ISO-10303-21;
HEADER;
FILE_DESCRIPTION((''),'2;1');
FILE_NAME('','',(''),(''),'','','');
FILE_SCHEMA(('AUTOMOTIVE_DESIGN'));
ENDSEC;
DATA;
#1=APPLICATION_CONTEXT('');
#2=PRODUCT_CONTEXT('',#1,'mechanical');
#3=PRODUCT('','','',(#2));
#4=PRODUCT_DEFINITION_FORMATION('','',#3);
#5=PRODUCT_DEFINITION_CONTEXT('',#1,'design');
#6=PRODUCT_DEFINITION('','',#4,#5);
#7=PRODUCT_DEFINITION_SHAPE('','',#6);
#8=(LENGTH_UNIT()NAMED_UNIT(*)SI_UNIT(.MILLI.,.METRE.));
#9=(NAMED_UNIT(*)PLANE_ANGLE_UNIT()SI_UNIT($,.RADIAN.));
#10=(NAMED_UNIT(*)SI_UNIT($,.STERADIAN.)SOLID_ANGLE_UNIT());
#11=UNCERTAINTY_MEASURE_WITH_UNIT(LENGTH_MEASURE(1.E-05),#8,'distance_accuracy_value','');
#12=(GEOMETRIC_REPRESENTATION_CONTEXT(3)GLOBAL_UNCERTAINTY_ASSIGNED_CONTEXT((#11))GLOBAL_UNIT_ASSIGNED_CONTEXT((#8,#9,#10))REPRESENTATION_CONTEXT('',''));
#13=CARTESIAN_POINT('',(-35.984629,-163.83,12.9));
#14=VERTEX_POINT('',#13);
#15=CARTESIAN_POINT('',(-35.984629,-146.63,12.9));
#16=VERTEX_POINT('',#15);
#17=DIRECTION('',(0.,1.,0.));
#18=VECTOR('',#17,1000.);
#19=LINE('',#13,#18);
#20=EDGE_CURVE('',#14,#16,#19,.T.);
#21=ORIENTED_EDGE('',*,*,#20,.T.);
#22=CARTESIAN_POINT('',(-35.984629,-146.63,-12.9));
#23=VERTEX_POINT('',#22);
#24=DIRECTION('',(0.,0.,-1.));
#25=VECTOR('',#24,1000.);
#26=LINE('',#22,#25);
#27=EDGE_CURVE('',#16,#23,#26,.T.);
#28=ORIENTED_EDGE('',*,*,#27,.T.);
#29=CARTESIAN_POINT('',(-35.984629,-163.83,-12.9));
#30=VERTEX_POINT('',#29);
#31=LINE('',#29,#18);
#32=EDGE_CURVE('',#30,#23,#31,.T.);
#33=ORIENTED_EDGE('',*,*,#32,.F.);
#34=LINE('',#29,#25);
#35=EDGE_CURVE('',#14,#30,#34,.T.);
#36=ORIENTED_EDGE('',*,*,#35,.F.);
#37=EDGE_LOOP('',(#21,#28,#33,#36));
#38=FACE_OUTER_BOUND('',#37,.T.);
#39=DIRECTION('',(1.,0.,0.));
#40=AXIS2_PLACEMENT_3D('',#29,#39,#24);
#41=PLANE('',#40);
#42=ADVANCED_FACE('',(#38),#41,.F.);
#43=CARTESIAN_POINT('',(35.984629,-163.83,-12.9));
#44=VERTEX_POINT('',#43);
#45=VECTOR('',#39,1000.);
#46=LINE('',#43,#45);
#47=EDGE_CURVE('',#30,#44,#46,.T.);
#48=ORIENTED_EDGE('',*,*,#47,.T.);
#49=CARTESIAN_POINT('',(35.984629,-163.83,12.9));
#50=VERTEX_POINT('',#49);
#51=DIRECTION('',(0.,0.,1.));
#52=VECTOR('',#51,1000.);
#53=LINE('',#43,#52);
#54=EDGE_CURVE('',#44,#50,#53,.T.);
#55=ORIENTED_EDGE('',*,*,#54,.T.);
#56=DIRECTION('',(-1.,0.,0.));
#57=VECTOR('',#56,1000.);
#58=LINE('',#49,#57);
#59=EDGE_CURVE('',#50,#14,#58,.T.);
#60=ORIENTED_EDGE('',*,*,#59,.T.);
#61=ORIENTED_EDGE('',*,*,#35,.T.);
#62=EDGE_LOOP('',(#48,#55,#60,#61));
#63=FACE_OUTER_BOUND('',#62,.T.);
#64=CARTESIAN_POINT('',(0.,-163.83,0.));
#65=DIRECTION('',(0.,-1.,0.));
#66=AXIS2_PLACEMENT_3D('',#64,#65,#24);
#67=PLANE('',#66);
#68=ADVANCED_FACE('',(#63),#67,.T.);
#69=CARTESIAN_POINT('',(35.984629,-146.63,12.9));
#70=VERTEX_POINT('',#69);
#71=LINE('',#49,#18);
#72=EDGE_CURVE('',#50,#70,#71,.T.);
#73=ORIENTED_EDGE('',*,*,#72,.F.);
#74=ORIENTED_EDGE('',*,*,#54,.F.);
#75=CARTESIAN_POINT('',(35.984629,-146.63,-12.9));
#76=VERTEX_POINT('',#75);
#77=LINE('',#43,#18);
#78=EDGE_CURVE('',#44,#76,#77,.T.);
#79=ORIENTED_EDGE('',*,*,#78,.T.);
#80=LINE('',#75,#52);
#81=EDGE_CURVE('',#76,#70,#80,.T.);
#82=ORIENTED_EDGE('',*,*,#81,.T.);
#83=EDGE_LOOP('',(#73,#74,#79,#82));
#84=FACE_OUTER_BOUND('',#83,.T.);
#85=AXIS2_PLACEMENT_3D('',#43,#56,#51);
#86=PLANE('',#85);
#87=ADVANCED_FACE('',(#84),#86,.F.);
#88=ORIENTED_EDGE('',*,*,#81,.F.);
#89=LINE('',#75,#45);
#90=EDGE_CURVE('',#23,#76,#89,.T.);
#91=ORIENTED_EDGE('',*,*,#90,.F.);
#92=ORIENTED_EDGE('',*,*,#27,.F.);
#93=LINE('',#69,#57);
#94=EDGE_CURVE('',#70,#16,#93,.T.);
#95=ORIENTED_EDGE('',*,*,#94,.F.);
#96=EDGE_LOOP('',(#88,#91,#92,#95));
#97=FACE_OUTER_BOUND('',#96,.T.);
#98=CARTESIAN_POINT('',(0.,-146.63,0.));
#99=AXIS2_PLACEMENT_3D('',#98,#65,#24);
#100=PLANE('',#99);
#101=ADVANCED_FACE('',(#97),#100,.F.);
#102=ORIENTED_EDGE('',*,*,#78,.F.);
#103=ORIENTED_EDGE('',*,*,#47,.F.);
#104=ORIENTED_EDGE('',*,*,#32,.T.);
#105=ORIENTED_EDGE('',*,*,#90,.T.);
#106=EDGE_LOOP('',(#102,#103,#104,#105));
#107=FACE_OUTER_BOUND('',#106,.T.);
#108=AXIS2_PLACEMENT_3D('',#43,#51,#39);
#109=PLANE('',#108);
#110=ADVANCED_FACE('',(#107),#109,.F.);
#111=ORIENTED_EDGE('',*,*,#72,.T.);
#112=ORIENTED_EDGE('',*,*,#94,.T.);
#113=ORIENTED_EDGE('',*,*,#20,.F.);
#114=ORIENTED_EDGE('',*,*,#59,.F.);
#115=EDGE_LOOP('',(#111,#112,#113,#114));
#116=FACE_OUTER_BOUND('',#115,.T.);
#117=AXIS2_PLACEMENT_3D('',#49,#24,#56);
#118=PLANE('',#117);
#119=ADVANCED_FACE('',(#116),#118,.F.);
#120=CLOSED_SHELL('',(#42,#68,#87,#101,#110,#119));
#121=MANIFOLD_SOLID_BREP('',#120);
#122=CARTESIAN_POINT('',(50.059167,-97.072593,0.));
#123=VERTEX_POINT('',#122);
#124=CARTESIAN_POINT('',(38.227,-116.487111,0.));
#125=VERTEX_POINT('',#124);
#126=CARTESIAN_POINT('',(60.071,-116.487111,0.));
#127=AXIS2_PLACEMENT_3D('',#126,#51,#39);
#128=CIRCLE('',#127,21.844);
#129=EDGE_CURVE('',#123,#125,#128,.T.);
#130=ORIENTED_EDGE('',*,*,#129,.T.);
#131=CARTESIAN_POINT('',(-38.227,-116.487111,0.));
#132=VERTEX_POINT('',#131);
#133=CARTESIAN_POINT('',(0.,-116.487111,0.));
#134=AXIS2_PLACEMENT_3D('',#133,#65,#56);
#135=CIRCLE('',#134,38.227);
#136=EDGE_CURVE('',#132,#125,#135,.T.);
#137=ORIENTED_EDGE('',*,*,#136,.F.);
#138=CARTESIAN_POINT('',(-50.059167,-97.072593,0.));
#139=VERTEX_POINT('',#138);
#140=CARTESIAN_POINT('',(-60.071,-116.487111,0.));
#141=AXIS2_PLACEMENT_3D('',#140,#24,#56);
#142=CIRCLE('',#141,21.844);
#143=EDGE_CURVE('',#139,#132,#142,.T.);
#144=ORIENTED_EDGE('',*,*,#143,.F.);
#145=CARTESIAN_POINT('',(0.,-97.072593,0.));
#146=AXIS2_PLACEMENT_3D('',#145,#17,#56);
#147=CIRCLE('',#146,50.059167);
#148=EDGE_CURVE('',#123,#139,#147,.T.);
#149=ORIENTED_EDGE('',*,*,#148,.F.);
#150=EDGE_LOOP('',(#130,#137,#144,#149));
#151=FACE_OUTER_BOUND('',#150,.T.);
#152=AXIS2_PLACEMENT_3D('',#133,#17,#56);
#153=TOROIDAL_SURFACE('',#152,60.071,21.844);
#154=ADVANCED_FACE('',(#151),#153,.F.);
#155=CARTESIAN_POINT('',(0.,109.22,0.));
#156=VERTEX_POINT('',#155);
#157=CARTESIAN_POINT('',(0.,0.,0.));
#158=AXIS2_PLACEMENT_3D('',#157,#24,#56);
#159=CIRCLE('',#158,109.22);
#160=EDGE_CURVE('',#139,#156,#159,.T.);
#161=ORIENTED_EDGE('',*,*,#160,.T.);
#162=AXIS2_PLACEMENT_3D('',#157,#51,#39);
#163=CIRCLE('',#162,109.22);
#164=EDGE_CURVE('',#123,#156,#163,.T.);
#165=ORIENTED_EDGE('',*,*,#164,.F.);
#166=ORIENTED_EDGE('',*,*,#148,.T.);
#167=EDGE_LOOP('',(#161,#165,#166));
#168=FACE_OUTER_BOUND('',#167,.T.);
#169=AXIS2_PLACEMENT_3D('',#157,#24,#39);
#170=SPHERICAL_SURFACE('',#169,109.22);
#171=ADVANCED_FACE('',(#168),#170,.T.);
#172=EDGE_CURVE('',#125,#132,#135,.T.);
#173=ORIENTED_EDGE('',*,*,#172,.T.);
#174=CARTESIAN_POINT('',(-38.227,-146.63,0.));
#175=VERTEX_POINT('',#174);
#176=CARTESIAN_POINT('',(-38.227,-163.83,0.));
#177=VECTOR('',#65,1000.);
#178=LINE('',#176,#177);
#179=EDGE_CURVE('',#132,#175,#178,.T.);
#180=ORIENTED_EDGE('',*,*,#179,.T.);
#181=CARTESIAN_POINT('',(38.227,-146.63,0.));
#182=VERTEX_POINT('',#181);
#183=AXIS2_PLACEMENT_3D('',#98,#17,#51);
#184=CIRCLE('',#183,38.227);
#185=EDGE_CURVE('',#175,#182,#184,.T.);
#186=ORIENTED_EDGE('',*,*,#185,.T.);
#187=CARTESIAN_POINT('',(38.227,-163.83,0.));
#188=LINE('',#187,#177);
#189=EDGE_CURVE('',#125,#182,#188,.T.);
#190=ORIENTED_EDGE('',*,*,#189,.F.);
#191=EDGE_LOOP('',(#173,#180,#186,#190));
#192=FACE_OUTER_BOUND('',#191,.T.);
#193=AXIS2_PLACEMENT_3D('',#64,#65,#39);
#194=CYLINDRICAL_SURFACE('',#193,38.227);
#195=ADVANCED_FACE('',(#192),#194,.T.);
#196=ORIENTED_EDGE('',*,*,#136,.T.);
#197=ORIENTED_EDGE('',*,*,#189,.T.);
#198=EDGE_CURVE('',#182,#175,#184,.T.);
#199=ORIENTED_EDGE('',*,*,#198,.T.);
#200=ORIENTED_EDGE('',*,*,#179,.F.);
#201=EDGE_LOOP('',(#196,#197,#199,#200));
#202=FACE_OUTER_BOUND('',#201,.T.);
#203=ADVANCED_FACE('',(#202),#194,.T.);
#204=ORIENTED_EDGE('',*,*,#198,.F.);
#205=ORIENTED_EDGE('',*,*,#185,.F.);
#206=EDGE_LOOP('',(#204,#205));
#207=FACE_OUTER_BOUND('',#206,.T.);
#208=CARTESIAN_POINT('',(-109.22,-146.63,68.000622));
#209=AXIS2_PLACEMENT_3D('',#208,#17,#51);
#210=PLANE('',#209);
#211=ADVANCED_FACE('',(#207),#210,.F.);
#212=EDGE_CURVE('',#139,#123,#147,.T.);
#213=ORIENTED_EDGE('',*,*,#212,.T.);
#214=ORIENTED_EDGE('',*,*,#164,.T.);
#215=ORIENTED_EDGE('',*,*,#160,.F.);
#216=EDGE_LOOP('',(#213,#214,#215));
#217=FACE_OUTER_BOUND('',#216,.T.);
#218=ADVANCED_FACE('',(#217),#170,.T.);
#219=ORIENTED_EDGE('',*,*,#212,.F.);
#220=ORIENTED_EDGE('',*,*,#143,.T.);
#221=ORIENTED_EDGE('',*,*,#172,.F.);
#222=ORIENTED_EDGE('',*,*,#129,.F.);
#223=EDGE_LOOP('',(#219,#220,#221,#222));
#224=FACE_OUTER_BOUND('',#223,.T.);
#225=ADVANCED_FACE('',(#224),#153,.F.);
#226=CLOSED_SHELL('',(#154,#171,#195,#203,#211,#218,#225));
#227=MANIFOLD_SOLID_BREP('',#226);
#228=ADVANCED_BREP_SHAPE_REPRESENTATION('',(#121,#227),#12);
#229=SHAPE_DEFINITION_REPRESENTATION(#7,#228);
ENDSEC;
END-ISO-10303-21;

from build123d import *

# Parameters (mm, degrees)
SKETCH2_W               = 4.445
SKETCH2_H               = 19.05
FILETE2_R               = 2.54
SKETCH7_T_R             = 6.35
SKETCH7_T_R_2           = 2.5
CUT_EXTRUDE4_T_DEPTH    = 25.4
CUT_EXTRUDE1_DEPTH      = 27.181720795
CUT_EXTRUDE1_DEPTH_BACK = 27.181720795
SKETCH_1_W              = 15.700965646
SKETCH_1_H              = 4.620140609
SKETCH_2_W              = 8.368518388
SKETCH_2_H              = 3
BOSS_EXTRUDE1_DEPTH     = 2
SCALE1_SCALE            = 8.6


with BuildPart() as part:
    # Sketch1 → Revolve1 (revolve)
    with BuildSketch(Plane.XY):
        with BuildLine():
            Line((0, 12.7), (0, -12.7))
            ThreePointArc((0, -12.7), (-12.7, 0), (0, 12.7))
        make_face()
    revolve(axis=Axis((0, 12.7, 0), (0, -1, 0)))

    # Sketch2 → Revolve2 (revolve)
    with BuildSketch(Plane.XY, mode=Mode.PRIVATE) as revolve2_sk:
        with Locations((-2.2225, -9.525)):
            Rectangle(SKETCH2_W, SKETCH2_H)
    revolve(revolve2_sk.sketch.rotate(Axis((0, -19.05, 0), (0, 1, 0)), 180), axis=Axis((0, -19.05, 0), (0, 1, 0)))

    # Filete2
    filete2_edges = [part.edges().sort_by_distance(p)[0] for p in [
        (0, -11.896721187, 4.445),
    ]]
    fillet(filete2_edges, radius=FILETE2_R)

    # Sketch7-T → Cut-Extrude4-T (cut, symmetric)
    with BuildSketch(Plane(origin=(0, 0, 0), x_dir=(0, 0, -1), z_dir=(1, 0, 0))):
        with Locations((0, -24.765)):
            Circle(SKETCH7_T_R)
        with Locations((0, -66.675)):
            Circle(SKETCH7_T_R_2)
    extrude(amount=CUT_EXTRUDE4_T_DEPTH, both=True, mode=Mode.SUBTRACT)

    # 草图1 → Cut-Extrude1 (cut, two sides: drawn at the far end of the back side and taken through both)
    with BuildSketch(Plane(origin=(0, 0, 0), x_dir=(0, 0, -1), z_dir=(1, 0, 0)).offset(-CUT_EXTRUDE1_DEPTH_BACK)):
        with Locations((-0.056566237, -19.360070304)):
            Rectangle(SKETCH_1_W, SKETCH_1_H)
    extrude(amount=CUT_EXTRUDE1_DEPTH + CUT_EXTRUDE1_DEPTH_BACK, mode=Mode.SUBTRACT)


with BuildPart() as body_2:
    # 草图2 → Boss-Extrude1 (new body)
    with BuildSketch(Plane.XZ.offset(17.05)):
        Rectangle(SKETCH_2_W, SKETCH_2_H)
    extrude(amount=BOSS_EXTRUDE1_DEPTH)


with BuildPart() as part_1:
    # Scale1: scaled about (0, 0, 0)
    add(part.part.scale(SCALE1_SCALE))


with BuildPart() as body_2_1:
    # Scale1: scaled about (0, 0, 0)
    add(body_2.part.scale(SCALE1_SCALE))


solid = Compound([part_1.part, body_2_1.part])
